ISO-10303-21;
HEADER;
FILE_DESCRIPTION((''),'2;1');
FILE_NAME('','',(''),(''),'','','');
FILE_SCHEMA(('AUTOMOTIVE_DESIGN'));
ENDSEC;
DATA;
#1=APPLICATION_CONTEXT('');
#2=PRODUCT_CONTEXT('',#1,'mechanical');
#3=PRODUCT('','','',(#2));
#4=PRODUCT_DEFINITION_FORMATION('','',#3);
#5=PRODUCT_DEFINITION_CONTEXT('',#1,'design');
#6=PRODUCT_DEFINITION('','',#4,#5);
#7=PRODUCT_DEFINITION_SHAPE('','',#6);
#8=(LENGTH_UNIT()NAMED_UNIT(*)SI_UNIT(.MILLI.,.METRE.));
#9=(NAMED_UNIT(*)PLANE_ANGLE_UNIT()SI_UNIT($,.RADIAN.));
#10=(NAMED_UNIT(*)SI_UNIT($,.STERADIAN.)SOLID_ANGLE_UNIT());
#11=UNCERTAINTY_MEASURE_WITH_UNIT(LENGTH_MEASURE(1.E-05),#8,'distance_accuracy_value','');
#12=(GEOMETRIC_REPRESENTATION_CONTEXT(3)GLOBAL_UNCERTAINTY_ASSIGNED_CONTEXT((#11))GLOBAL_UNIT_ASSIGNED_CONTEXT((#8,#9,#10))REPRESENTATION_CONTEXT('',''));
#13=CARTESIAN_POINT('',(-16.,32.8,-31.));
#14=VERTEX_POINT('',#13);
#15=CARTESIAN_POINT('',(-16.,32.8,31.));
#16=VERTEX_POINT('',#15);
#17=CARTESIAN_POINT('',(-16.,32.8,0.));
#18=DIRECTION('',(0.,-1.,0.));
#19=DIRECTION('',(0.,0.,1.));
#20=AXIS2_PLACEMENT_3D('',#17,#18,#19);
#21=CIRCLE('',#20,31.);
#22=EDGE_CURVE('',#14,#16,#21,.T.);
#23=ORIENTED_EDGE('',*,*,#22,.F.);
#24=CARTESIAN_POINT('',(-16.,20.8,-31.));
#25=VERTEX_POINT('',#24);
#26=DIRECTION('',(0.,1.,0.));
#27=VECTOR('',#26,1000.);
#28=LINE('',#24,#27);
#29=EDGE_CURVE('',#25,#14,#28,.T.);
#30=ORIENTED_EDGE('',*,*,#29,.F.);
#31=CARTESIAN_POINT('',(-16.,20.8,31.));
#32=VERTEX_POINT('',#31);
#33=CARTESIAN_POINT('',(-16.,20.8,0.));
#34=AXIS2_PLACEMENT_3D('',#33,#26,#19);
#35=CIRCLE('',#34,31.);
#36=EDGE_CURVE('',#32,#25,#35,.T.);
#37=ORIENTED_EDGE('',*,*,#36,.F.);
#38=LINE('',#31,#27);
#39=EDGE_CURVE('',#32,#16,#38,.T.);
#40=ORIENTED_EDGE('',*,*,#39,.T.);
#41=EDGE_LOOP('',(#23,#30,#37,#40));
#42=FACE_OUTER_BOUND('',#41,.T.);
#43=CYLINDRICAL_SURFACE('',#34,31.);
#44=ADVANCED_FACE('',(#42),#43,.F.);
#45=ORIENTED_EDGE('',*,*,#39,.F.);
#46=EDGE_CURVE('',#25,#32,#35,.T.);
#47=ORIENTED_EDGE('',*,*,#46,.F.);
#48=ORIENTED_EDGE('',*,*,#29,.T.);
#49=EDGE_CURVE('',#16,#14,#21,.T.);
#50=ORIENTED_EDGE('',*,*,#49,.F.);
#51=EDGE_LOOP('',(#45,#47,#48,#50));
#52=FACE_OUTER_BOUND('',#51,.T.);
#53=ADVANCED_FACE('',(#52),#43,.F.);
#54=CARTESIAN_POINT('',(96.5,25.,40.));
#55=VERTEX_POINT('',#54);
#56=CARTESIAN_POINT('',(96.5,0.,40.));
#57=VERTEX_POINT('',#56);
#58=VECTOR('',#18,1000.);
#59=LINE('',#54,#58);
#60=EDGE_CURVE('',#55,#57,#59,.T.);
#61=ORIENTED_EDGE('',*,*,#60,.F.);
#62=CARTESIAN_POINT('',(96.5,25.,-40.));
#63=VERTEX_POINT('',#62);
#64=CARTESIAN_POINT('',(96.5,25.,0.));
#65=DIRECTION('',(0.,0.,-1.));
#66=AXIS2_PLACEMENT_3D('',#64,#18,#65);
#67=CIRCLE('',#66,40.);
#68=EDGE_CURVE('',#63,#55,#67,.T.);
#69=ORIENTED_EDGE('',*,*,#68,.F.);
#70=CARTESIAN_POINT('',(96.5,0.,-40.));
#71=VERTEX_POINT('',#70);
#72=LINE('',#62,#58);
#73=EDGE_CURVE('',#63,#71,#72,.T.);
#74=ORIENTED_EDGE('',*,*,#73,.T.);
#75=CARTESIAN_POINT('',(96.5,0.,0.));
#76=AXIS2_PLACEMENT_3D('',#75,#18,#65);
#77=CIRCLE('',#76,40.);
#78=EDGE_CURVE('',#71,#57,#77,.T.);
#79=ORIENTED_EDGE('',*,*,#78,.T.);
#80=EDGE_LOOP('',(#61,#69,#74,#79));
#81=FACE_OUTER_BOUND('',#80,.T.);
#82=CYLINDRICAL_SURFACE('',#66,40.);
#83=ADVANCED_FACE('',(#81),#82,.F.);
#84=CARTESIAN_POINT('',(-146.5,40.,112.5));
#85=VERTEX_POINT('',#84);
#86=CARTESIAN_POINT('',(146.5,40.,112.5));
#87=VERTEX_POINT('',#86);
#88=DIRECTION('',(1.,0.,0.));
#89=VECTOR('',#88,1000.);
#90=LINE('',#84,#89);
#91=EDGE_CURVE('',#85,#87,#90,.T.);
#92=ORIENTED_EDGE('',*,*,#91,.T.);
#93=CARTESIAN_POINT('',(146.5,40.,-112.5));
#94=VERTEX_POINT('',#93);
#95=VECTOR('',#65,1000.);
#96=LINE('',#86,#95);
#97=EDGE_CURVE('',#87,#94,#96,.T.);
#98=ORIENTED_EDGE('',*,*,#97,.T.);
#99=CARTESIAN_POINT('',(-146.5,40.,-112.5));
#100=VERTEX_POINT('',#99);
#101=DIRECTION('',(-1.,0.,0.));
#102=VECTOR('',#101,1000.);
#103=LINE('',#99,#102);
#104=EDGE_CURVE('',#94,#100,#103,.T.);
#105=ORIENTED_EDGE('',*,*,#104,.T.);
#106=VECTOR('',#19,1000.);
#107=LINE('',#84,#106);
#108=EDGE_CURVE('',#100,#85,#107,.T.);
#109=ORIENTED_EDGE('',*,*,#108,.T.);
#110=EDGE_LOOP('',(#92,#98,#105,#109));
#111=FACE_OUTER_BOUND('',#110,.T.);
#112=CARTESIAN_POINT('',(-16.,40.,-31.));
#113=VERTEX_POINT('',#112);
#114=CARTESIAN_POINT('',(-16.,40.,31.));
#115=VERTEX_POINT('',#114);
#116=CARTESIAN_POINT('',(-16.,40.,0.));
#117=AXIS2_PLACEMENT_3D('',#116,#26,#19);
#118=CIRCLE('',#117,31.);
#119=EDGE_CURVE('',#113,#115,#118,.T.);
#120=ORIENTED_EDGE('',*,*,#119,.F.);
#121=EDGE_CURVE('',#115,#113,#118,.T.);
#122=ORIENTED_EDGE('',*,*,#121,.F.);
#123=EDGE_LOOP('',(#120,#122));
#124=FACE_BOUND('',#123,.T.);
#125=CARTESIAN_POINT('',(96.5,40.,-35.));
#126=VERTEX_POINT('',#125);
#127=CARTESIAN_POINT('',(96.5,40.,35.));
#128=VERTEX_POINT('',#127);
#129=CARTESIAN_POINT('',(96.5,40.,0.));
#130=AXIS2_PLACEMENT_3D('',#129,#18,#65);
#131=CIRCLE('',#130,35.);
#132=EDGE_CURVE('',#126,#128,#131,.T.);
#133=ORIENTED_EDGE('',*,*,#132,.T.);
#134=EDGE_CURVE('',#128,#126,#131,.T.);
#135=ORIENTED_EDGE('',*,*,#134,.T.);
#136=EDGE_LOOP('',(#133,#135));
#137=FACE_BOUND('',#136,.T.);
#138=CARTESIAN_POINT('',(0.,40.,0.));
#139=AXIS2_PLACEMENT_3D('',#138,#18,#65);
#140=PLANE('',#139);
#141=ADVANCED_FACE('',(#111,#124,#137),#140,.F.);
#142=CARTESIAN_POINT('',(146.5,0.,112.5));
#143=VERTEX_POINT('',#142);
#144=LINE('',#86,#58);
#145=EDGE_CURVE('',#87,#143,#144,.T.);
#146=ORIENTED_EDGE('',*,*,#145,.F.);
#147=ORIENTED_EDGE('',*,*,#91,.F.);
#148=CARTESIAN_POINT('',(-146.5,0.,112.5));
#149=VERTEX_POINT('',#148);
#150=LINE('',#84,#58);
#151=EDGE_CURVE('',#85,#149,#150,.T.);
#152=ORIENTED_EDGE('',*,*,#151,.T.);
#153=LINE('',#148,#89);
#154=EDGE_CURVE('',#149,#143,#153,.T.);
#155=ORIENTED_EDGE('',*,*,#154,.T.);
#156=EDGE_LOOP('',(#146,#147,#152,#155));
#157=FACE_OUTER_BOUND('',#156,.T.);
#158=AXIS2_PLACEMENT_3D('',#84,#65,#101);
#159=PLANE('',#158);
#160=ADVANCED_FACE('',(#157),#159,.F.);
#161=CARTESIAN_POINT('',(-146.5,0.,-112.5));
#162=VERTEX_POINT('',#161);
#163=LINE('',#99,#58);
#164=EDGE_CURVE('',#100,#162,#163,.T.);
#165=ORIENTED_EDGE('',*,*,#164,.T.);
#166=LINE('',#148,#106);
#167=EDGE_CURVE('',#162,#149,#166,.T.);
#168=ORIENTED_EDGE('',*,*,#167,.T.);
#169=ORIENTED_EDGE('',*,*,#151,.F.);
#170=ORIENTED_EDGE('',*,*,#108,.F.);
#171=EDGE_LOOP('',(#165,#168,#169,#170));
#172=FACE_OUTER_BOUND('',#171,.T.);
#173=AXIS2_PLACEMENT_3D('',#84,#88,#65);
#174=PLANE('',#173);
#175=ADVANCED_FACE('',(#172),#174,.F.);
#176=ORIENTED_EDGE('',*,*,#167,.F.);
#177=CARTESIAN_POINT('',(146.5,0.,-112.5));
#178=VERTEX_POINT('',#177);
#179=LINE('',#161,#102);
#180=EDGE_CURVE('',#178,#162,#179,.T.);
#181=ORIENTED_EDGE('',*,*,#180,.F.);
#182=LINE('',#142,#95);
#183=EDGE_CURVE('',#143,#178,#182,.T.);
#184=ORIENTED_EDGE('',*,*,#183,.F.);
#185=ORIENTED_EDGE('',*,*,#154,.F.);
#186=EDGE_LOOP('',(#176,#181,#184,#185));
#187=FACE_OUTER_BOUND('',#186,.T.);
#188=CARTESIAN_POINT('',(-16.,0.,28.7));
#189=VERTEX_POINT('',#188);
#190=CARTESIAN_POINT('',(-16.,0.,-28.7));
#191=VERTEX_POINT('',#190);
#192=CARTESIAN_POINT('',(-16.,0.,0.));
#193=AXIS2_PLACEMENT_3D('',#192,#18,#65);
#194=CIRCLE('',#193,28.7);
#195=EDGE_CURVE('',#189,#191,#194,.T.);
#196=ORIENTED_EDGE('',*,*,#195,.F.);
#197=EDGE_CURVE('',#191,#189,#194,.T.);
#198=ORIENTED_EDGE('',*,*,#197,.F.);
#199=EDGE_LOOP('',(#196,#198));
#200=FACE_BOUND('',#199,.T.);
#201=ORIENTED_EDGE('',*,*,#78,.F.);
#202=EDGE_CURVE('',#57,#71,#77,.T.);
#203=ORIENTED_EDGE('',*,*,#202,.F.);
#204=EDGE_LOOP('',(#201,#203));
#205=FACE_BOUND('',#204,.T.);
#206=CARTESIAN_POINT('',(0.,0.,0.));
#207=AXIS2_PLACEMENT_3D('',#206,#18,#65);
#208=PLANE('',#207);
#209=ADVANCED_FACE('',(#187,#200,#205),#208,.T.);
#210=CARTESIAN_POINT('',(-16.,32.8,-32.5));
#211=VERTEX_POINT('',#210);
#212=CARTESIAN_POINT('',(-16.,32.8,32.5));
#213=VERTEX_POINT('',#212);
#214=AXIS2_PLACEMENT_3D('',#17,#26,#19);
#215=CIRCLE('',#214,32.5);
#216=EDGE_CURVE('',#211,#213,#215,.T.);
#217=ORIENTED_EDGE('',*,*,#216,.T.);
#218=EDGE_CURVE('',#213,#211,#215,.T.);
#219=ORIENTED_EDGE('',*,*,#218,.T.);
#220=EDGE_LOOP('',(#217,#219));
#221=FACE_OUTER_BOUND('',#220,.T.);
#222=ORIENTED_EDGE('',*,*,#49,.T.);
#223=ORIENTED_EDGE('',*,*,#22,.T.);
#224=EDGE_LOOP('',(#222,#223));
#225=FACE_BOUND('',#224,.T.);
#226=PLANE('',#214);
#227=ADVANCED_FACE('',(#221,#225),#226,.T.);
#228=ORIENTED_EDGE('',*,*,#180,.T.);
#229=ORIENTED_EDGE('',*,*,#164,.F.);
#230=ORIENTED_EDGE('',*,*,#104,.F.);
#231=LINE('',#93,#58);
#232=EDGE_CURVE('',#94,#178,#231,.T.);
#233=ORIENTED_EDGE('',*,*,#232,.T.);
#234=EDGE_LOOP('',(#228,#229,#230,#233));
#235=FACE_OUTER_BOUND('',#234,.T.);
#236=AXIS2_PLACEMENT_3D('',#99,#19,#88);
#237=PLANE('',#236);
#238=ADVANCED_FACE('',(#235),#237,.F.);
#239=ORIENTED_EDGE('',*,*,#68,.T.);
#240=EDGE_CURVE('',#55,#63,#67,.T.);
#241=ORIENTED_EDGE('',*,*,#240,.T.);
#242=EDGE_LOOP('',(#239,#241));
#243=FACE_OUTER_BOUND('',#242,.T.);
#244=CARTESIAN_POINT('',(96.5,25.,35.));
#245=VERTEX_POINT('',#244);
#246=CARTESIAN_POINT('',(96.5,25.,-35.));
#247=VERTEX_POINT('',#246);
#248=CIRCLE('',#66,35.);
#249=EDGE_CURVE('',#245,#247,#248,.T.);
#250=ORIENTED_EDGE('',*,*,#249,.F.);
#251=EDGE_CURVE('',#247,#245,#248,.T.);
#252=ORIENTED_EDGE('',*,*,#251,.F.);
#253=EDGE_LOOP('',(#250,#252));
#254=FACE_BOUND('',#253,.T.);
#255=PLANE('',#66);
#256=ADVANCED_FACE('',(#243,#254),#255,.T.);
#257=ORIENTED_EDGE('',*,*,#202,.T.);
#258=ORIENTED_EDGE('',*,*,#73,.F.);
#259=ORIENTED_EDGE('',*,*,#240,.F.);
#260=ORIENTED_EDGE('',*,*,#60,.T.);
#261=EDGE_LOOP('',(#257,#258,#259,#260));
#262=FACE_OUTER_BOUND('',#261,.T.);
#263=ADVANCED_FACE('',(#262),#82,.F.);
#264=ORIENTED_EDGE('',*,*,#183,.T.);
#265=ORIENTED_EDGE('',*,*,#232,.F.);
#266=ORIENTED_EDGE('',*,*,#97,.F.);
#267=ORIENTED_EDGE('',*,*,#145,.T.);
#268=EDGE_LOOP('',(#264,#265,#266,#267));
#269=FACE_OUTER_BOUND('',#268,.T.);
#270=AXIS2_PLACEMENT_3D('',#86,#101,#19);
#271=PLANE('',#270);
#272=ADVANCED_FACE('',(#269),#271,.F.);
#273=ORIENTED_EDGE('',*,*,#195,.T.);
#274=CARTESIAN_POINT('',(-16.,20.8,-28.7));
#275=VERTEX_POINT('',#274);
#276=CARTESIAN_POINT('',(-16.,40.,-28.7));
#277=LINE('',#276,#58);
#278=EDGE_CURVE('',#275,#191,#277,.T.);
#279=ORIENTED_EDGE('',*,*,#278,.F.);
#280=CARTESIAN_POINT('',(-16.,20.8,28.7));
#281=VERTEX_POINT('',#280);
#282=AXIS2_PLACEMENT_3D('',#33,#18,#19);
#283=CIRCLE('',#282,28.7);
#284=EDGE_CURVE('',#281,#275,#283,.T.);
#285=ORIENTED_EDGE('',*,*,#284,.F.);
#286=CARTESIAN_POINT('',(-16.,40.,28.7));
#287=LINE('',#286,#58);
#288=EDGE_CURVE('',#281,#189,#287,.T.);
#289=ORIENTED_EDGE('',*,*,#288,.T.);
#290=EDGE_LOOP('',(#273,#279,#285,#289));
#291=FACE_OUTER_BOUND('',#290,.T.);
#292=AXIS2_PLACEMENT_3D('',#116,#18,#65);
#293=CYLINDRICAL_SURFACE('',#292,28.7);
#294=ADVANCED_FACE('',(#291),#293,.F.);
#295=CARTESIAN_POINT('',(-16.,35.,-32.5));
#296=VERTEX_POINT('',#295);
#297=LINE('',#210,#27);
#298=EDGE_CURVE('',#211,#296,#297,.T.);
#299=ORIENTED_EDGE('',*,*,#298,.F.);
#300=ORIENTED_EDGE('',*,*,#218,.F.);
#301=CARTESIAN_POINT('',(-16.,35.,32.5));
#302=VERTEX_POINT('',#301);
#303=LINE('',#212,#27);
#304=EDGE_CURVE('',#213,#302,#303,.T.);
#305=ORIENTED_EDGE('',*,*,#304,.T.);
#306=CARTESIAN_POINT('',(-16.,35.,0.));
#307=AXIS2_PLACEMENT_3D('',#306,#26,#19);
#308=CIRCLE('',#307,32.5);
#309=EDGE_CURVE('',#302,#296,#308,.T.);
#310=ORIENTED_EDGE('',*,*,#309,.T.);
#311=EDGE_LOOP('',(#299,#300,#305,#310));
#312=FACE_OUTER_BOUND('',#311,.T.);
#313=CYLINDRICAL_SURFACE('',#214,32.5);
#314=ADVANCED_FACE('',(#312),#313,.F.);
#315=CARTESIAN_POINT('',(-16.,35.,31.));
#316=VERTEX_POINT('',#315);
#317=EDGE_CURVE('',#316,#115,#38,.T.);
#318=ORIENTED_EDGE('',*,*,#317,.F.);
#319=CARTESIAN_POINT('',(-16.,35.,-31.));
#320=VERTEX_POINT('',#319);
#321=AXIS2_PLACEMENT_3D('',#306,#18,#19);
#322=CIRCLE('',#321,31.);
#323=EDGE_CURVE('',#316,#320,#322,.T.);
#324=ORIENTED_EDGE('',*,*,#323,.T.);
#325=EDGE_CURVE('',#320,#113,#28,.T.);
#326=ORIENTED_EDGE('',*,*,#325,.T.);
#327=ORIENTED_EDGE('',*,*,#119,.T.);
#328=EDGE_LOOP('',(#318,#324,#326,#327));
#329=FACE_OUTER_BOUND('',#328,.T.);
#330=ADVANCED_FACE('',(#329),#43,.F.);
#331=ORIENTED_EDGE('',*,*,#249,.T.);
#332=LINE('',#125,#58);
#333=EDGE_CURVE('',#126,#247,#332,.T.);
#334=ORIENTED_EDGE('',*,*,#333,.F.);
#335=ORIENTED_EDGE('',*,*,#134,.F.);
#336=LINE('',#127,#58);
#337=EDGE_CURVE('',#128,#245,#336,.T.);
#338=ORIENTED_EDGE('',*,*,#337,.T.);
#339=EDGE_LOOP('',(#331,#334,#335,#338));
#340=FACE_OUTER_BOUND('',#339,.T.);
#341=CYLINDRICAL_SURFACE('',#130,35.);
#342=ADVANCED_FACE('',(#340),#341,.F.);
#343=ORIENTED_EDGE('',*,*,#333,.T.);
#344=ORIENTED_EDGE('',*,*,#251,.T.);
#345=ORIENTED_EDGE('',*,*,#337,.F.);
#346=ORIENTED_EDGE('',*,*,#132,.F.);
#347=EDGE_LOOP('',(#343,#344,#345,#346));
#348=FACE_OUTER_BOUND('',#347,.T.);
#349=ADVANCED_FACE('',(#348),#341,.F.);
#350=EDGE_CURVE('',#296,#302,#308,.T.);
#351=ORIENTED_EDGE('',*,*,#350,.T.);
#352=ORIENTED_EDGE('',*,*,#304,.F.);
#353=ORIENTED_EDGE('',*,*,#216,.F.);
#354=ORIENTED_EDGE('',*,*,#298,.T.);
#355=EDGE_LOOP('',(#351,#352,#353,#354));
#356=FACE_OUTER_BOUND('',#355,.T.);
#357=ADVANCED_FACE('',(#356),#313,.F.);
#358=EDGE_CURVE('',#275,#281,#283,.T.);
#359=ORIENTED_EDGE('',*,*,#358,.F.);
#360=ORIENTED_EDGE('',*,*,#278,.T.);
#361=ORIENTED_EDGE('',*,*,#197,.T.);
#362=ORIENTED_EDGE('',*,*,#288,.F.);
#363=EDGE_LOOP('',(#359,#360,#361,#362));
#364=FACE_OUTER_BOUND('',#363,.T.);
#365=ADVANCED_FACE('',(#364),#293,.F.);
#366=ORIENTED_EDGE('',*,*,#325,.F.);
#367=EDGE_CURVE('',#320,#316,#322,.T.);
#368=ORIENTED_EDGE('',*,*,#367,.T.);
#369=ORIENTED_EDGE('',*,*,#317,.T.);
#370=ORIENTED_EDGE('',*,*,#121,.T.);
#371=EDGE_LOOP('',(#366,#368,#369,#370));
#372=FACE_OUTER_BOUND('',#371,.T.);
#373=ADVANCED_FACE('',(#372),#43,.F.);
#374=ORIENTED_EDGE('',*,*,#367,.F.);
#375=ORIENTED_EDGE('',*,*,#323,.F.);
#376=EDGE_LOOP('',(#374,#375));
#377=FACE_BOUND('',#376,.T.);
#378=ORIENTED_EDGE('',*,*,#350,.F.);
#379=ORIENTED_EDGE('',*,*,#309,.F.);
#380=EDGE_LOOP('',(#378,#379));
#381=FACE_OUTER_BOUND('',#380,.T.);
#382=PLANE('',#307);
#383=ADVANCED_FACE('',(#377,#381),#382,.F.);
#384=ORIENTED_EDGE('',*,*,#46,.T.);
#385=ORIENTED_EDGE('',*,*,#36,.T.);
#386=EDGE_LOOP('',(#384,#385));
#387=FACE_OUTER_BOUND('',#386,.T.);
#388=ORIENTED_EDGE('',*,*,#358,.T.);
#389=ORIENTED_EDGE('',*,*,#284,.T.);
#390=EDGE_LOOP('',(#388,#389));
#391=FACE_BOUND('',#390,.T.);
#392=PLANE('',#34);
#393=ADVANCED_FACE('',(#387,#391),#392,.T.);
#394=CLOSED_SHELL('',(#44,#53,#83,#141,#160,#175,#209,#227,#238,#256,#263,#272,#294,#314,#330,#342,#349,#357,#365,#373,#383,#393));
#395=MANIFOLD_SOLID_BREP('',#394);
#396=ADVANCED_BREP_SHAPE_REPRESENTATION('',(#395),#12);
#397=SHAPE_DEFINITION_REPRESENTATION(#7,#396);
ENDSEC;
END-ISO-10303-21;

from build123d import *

# Parameters (mm, degrees)
SKETCH_1_W          = 293
SKETCH_1_H          = 225
EXTRUDE_1_DEPTH     = 40
SKETCH_2_R          = 40
CUT_EXTRUDE_1_DEPTH = 25
SKETCH_3_R          = 28.7
CUT_EXTRUDE_2_DEPTH = 189.993386128
SKETCH_4_R          = 35
CUT_EXTRUDE_3_DEPTH = 189.993386128
SKETCH_5_R          = 31
CUT_EXTRUDE_4_DEPTH = 19.2
SKETCH_6_R          = 32.5
CUT_EXTRUDE_5_DEPTH = 2.2


with BuildPart() as part:
    # 草图1 → 凸台-拉伸1 (new body)
    with BuildSketch(Plane(origin=(0, 0, 0), x_dir=(1, 0, 0), z_dir=(0, 1, 0))):
        Rectangle(SKETCH_1_W, SKETCH_1_H)
    extrude(amount=EXTRUDE_1_DEPTH)

    # 草图2 → 切除-拉伸1 (cut)
    with BuildSketch(Plane.XZ):
        with Locations(Location((96.5, 0, 0), (0, 0, 270))):
            Circle(SKETCH_2_R)
    extrude(amount=-CUT_EXTRUDE_1_DEPTH, mode=Mode.SUBTRACT)

    # 草图3 → 切除-拉伸2 (cut, through all)
    with BuildSketch(Plane.XZ):
        with Locations(Location((-16, 0, 0), (0, 0, 270))):
            Circle(SKETCH_3_R)
    extrude(amount=-CUT_EXTRUDE_2_DEPTH, mode=Mode.SUBTRACT)

    # 草图4 → 切除-拉伸3 (cut, through all)
    with BuildSketch(Plane.XZ):
        with Locations(Location((96.5, 0, 0), (0, 0, 270))):
            Circle(SKETCH_4_R)
    extrude(amount=-CUT_EXTRUDE_3_DEPTH, mode=Mode.SUBTRACT)

    # 草图5 → 切除-拉伸4 (cut)
    with BuildSketch(Plane(origin=(0, 40, 0), x_dir=(1, 0, 0), z_dir=(0, 1, 0))):
        with Locations(Location((-16, 0, 0), (0, 0, 270))):
            Circle(SKETCH_5_R)
    extrude(amount=-CUT_EXTRUDE_4_DEPTH, mode=Mode.SUBTRACT)

    # 草图6 → 切除-拉伸5 (cut)
    with BuildSketch(Plane(origin=(0, 35, 0), x_dir=(1, 0, 0), z_dir=(0, 1, 0))):
        with Locations(Location((-16, 0, 0), (0, 0, 270))):
            Circle(SKETCH_6_R)
    extrude(amount=-CUT_EXTRUDE_5_DEPTH, mode=Mode.SUBTRACT)


solid = part.part
